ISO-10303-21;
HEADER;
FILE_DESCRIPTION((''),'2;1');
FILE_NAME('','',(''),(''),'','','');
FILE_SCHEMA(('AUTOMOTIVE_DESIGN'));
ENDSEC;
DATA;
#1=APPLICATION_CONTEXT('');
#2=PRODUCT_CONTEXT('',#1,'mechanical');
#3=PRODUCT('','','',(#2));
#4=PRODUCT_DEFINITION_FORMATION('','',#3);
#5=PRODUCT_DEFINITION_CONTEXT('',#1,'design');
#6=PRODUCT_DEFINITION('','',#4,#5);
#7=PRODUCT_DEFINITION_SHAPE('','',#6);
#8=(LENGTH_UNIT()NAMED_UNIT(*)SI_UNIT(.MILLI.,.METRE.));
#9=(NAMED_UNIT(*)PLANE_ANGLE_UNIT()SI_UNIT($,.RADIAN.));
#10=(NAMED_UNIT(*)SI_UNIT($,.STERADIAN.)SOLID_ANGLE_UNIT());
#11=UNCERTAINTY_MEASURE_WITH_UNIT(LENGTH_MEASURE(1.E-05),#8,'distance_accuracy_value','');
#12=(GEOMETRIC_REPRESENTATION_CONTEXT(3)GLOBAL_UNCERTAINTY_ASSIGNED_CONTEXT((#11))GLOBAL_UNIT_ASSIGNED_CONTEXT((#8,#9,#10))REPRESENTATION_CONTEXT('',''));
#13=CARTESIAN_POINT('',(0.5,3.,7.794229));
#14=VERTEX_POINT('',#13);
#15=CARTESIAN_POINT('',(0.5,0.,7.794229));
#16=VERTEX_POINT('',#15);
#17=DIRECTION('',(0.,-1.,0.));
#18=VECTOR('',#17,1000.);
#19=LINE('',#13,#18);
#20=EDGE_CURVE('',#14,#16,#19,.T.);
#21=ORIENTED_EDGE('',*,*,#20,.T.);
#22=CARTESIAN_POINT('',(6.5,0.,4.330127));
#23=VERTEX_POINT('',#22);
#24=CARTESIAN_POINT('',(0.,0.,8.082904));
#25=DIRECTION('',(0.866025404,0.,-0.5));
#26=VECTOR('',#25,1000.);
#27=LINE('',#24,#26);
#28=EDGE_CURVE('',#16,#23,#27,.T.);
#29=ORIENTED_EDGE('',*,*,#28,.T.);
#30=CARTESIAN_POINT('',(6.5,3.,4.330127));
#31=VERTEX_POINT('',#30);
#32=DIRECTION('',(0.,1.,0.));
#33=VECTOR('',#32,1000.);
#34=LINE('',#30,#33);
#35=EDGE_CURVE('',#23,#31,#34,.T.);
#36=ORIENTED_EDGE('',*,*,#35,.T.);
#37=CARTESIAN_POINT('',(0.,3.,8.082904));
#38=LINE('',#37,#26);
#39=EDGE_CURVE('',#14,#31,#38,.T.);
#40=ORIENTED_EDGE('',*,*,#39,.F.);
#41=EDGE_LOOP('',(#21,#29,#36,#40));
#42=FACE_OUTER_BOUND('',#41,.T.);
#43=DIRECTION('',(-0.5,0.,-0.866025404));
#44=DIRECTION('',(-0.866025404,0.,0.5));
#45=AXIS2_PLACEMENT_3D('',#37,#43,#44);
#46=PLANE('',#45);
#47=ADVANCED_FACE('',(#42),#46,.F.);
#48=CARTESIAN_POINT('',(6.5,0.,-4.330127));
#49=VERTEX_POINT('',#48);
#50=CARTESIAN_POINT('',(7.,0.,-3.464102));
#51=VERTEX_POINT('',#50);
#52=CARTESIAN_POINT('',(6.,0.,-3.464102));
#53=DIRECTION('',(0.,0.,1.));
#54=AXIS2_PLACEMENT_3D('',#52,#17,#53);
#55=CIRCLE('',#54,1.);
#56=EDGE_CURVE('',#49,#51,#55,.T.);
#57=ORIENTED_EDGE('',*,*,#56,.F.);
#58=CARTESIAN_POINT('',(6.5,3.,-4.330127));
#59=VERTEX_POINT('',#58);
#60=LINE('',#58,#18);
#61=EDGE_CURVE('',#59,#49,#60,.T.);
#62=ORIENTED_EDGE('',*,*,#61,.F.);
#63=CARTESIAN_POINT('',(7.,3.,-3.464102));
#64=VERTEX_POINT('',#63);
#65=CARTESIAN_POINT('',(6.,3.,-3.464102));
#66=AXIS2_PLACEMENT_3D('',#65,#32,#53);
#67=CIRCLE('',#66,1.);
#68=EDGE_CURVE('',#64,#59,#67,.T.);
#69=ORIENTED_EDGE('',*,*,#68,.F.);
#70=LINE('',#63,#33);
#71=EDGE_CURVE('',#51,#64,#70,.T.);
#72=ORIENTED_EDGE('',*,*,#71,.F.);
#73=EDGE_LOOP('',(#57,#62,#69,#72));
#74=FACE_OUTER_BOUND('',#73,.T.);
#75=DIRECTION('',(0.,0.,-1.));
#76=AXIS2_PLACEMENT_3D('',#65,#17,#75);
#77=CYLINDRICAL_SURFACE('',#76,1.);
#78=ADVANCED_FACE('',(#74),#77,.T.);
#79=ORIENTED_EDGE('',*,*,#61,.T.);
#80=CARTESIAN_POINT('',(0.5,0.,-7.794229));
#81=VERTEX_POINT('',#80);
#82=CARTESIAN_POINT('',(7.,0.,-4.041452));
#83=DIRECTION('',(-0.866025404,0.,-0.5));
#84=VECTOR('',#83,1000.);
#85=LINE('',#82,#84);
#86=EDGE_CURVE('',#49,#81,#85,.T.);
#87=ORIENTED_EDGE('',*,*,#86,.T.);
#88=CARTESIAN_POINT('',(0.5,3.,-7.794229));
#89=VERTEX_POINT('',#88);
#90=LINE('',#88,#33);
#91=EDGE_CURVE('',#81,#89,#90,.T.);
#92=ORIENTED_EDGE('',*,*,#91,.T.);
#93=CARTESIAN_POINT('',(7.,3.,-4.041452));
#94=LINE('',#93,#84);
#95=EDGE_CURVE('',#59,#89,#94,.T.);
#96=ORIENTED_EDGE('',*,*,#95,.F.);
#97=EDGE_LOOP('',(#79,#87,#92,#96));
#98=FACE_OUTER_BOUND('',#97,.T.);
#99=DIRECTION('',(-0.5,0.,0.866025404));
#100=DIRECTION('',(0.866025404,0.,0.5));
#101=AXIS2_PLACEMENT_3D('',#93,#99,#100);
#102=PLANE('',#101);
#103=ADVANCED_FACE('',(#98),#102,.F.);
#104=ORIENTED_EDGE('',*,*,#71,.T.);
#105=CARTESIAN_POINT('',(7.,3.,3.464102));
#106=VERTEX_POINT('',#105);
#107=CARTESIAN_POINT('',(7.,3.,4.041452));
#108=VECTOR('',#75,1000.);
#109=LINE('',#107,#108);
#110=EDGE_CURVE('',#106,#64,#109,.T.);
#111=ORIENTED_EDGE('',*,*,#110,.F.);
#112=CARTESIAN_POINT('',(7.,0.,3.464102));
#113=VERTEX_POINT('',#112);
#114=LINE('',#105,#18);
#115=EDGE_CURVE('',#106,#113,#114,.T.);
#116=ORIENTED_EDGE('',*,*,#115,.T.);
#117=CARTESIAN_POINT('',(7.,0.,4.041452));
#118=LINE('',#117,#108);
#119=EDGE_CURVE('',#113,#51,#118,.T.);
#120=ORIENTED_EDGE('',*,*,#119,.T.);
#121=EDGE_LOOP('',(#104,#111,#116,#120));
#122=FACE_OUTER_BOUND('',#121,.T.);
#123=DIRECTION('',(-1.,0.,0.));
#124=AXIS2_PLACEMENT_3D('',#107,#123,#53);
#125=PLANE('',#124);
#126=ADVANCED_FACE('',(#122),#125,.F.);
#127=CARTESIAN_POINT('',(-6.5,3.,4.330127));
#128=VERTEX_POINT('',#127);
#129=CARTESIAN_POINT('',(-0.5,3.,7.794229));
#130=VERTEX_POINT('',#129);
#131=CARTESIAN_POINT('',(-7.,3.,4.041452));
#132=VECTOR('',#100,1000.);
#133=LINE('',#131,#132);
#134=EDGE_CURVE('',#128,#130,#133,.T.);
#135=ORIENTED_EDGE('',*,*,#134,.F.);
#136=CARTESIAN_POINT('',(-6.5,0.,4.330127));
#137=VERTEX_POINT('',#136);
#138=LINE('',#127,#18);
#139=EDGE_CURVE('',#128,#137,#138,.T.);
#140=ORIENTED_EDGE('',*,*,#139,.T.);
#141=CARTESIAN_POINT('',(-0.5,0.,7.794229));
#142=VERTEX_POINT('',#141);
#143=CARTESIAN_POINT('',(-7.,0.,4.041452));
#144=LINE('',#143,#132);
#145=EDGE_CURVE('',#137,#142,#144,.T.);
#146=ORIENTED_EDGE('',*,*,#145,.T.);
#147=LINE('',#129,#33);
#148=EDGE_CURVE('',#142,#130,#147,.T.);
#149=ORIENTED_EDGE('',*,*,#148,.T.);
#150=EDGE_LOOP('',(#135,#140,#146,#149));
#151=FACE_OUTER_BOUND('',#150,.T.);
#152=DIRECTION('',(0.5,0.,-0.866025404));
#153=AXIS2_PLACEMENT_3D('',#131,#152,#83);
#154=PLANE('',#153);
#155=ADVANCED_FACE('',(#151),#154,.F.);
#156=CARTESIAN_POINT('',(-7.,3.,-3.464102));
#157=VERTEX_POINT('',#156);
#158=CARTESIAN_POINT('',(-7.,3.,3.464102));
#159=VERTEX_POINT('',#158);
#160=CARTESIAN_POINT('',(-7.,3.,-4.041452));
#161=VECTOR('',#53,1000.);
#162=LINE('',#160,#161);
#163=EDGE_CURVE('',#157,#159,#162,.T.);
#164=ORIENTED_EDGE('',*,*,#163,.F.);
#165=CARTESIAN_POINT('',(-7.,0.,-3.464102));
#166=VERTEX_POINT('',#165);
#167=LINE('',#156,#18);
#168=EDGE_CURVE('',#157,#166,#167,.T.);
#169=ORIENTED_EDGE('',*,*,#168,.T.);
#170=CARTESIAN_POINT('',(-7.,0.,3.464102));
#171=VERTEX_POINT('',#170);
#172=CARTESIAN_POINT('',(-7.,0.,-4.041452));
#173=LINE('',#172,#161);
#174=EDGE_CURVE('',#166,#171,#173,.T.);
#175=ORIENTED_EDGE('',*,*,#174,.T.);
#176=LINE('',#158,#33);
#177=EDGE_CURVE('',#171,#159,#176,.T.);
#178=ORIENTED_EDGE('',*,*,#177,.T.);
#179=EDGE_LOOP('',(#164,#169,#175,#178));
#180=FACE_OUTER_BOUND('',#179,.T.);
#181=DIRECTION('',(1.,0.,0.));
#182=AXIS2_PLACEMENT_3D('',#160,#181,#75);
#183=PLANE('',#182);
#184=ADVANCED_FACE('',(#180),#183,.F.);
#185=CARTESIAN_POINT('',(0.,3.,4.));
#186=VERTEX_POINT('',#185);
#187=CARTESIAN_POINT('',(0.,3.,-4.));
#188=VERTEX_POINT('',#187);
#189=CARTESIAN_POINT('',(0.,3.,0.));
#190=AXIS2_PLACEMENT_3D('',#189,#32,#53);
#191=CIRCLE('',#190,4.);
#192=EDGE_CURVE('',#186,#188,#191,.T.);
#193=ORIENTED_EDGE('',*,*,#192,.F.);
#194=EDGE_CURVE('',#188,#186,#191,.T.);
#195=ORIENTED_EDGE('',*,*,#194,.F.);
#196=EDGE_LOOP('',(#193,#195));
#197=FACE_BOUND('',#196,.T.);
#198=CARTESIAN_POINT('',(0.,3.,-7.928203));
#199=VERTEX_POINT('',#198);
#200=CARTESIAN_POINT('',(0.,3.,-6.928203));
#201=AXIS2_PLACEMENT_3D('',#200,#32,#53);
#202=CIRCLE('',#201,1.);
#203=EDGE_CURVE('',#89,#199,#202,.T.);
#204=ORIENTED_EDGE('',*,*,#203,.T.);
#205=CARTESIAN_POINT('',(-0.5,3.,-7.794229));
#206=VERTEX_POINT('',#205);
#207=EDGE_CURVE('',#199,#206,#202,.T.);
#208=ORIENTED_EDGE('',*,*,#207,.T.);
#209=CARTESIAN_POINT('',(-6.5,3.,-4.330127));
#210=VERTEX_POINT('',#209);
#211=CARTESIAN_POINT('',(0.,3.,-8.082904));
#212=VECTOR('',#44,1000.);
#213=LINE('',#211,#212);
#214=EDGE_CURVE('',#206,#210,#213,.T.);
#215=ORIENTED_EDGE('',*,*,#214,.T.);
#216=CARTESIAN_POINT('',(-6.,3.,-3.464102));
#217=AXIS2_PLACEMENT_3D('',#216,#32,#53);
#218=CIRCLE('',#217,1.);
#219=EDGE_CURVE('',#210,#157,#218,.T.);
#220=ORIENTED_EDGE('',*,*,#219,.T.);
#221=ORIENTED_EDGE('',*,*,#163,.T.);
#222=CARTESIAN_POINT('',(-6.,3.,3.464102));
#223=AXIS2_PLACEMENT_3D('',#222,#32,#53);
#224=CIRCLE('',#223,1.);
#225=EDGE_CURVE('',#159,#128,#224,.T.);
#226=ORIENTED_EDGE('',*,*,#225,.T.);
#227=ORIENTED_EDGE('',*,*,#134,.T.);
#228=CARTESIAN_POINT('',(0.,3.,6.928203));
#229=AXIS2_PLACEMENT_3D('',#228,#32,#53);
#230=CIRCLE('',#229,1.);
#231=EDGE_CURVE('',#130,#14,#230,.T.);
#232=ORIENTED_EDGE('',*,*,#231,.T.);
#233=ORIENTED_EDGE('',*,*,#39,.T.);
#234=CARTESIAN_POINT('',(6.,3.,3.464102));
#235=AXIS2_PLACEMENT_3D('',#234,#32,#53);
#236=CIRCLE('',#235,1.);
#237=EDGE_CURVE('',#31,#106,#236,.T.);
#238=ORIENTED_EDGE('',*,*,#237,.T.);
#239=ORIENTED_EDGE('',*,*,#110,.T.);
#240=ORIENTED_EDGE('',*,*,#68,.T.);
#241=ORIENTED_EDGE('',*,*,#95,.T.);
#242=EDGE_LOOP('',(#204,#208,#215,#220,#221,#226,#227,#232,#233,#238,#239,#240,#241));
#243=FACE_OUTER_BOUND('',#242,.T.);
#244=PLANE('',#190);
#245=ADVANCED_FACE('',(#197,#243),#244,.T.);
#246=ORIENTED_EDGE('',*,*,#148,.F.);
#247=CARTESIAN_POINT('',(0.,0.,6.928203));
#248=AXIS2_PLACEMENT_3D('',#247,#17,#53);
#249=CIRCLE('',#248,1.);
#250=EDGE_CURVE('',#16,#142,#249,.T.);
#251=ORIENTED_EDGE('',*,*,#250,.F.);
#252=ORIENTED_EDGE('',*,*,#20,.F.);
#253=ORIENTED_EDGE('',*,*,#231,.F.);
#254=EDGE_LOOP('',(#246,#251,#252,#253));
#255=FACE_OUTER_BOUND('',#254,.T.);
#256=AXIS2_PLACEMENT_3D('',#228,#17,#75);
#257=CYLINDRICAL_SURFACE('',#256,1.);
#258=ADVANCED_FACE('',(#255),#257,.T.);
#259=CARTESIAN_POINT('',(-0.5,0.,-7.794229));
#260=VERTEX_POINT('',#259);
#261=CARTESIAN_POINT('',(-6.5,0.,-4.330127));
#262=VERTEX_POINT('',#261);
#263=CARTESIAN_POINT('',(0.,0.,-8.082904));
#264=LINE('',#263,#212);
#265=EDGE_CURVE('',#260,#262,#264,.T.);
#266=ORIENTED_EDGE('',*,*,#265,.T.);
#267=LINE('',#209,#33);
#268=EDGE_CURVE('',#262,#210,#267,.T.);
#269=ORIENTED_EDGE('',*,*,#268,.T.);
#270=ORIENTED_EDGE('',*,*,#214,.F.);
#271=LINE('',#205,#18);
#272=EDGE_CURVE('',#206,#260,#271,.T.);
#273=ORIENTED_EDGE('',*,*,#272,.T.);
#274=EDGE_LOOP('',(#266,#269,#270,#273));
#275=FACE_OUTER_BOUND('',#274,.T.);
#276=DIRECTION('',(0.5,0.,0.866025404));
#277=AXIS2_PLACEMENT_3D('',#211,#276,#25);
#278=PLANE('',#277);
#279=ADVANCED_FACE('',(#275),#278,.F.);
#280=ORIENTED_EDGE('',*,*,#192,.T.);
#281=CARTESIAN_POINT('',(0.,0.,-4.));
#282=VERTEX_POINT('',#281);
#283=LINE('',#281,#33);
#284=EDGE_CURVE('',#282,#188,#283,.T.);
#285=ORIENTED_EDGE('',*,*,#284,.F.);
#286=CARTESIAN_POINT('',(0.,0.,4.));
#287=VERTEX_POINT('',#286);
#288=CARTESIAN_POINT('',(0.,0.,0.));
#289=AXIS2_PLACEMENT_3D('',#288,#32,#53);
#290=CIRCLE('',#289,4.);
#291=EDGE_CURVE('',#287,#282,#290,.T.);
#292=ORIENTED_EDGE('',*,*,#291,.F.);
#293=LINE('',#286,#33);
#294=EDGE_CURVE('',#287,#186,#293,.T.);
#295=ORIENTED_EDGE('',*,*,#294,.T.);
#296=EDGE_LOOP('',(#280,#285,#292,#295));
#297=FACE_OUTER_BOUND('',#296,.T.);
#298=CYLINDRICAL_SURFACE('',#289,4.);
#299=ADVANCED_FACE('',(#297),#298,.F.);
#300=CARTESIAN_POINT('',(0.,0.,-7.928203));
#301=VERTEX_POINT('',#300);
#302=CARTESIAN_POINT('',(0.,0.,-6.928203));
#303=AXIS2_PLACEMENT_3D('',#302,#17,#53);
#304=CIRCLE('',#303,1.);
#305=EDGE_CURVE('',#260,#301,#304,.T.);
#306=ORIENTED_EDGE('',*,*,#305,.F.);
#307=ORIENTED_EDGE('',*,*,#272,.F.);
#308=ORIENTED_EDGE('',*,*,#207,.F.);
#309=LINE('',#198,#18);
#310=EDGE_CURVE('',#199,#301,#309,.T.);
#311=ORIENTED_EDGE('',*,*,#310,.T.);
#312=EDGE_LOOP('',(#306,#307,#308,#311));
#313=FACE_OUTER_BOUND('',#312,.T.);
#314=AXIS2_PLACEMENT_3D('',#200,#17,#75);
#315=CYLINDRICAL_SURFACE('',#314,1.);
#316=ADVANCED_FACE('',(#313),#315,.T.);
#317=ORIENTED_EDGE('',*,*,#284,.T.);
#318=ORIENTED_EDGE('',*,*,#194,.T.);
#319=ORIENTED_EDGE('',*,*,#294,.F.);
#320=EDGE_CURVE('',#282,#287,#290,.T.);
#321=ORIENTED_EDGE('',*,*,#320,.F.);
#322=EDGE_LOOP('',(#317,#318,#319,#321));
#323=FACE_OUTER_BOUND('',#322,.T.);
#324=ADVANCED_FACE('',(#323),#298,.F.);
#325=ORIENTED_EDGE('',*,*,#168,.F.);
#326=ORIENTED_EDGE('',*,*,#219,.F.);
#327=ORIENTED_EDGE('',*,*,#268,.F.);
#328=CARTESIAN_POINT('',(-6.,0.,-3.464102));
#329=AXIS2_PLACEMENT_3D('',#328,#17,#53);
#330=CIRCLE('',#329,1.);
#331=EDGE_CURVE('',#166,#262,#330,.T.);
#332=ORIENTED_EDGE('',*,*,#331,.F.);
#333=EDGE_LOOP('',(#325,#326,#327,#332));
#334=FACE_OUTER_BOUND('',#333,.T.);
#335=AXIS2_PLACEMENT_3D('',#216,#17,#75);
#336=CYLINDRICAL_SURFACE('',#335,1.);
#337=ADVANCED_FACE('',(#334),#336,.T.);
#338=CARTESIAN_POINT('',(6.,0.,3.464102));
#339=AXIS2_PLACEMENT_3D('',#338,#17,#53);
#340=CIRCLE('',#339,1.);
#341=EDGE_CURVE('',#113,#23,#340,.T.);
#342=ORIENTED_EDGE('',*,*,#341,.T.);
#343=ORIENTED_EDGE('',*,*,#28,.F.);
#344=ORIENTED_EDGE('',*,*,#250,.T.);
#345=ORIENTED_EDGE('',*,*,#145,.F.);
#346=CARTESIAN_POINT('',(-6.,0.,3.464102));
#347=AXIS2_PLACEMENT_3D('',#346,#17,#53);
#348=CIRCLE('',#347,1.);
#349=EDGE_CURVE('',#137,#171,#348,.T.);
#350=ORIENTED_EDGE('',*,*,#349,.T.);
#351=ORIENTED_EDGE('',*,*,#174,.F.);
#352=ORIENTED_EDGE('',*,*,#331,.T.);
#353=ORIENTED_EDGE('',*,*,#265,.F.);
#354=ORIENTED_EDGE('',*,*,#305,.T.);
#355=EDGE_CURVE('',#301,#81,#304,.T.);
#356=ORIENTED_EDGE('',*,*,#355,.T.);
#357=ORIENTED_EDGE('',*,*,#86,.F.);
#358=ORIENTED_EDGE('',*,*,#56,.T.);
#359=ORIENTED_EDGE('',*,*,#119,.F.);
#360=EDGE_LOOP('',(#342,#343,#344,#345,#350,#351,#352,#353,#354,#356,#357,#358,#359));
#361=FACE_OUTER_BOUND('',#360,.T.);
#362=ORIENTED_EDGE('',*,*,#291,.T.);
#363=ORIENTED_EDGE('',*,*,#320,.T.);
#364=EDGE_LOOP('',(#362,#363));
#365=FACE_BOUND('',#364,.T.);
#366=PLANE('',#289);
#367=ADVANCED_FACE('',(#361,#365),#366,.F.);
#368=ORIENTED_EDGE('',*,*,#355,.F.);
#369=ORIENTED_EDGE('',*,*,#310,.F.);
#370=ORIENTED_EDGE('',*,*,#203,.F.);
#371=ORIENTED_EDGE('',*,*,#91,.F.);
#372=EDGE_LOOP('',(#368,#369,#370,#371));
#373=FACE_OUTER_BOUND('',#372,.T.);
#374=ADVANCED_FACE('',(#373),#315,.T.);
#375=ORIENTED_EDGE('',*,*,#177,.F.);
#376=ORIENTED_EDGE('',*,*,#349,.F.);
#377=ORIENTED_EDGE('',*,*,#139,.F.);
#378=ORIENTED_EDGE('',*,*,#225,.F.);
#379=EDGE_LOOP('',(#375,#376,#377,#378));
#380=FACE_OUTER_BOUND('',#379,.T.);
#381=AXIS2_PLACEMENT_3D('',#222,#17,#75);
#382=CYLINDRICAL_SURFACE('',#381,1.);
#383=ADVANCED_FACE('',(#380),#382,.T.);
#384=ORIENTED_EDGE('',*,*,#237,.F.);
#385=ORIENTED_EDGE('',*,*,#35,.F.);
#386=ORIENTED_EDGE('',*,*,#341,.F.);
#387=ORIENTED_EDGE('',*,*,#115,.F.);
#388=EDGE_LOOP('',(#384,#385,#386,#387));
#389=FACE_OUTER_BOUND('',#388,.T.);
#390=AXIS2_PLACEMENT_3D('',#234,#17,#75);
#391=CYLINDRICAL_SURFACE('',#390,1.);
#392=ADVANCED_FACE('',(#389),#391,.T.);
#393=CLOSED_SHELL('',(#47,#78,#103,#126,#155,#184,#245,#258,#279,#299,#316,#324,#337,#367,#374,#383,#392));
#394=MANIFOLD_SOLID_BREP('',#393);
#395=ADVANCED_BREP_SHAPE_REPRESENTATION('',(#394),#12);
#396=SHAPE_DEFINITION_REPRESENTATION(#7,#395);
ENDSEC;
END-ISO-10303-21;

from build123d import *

# Parameters (mm, degrees)
HEX_BODY_3MM_DEPTH      = 3
BORE_PROFILE_8_R        = 4
BORE_8_DEPTH            = 3
HEX_CORNER_FILLETS_R1_R = 1


with BuildPart() as part:
    # Hex Profile 14AF → Hex Body 3mm (new body)
    with BuildSketch(Plane(origin=(0, 0, 0), x_dir=(1, 0, 0), z_dir=(0, 1, 0))):
        Polygon((0, 8.082903769), (-7, 4.041451884), (-7, -4.041451884), (0, -8.082903769), (7, -4.041451884), (7, 4.041451884), align=None)
    extrude(amount=HEX_BODY_3MM_DEPTH)

    # Bore Profile Ø8 → Bore Ø8 (cut)
    with BuildSketch(Plane(origin=(0, 3, 0), x_dir=(1, 0, 0), z_dir=(0, 1, 0))):
        with Locations(Location((0, 0, 0), (0, 0, 270))):
            Circle(BORE_PROFILE_8_R)
    extrude(amount=-BORE_8_DEPTH, mode=Mode.SUBTRACT)

    # Hex Corner Fillets R1
    hex_corner_fillets_r1_edges = [part.edges().sort_by_distance(p)[0] for p in [
        (7, 1.5, -4.041451884),
        (7, 1.5, 4.041451884),
        (0, 1.5, 8.082903769),
        (-7, 1.5, 4.041451884),
        (-7, 1.5, -4.041451884),
        (0, 1.5, -8.082903769),
    ]]
    fillet(hex_corner_fillets_r1_edges, radius=HEX_CORNER_FILLETS_R1_R)


solid = part.part
